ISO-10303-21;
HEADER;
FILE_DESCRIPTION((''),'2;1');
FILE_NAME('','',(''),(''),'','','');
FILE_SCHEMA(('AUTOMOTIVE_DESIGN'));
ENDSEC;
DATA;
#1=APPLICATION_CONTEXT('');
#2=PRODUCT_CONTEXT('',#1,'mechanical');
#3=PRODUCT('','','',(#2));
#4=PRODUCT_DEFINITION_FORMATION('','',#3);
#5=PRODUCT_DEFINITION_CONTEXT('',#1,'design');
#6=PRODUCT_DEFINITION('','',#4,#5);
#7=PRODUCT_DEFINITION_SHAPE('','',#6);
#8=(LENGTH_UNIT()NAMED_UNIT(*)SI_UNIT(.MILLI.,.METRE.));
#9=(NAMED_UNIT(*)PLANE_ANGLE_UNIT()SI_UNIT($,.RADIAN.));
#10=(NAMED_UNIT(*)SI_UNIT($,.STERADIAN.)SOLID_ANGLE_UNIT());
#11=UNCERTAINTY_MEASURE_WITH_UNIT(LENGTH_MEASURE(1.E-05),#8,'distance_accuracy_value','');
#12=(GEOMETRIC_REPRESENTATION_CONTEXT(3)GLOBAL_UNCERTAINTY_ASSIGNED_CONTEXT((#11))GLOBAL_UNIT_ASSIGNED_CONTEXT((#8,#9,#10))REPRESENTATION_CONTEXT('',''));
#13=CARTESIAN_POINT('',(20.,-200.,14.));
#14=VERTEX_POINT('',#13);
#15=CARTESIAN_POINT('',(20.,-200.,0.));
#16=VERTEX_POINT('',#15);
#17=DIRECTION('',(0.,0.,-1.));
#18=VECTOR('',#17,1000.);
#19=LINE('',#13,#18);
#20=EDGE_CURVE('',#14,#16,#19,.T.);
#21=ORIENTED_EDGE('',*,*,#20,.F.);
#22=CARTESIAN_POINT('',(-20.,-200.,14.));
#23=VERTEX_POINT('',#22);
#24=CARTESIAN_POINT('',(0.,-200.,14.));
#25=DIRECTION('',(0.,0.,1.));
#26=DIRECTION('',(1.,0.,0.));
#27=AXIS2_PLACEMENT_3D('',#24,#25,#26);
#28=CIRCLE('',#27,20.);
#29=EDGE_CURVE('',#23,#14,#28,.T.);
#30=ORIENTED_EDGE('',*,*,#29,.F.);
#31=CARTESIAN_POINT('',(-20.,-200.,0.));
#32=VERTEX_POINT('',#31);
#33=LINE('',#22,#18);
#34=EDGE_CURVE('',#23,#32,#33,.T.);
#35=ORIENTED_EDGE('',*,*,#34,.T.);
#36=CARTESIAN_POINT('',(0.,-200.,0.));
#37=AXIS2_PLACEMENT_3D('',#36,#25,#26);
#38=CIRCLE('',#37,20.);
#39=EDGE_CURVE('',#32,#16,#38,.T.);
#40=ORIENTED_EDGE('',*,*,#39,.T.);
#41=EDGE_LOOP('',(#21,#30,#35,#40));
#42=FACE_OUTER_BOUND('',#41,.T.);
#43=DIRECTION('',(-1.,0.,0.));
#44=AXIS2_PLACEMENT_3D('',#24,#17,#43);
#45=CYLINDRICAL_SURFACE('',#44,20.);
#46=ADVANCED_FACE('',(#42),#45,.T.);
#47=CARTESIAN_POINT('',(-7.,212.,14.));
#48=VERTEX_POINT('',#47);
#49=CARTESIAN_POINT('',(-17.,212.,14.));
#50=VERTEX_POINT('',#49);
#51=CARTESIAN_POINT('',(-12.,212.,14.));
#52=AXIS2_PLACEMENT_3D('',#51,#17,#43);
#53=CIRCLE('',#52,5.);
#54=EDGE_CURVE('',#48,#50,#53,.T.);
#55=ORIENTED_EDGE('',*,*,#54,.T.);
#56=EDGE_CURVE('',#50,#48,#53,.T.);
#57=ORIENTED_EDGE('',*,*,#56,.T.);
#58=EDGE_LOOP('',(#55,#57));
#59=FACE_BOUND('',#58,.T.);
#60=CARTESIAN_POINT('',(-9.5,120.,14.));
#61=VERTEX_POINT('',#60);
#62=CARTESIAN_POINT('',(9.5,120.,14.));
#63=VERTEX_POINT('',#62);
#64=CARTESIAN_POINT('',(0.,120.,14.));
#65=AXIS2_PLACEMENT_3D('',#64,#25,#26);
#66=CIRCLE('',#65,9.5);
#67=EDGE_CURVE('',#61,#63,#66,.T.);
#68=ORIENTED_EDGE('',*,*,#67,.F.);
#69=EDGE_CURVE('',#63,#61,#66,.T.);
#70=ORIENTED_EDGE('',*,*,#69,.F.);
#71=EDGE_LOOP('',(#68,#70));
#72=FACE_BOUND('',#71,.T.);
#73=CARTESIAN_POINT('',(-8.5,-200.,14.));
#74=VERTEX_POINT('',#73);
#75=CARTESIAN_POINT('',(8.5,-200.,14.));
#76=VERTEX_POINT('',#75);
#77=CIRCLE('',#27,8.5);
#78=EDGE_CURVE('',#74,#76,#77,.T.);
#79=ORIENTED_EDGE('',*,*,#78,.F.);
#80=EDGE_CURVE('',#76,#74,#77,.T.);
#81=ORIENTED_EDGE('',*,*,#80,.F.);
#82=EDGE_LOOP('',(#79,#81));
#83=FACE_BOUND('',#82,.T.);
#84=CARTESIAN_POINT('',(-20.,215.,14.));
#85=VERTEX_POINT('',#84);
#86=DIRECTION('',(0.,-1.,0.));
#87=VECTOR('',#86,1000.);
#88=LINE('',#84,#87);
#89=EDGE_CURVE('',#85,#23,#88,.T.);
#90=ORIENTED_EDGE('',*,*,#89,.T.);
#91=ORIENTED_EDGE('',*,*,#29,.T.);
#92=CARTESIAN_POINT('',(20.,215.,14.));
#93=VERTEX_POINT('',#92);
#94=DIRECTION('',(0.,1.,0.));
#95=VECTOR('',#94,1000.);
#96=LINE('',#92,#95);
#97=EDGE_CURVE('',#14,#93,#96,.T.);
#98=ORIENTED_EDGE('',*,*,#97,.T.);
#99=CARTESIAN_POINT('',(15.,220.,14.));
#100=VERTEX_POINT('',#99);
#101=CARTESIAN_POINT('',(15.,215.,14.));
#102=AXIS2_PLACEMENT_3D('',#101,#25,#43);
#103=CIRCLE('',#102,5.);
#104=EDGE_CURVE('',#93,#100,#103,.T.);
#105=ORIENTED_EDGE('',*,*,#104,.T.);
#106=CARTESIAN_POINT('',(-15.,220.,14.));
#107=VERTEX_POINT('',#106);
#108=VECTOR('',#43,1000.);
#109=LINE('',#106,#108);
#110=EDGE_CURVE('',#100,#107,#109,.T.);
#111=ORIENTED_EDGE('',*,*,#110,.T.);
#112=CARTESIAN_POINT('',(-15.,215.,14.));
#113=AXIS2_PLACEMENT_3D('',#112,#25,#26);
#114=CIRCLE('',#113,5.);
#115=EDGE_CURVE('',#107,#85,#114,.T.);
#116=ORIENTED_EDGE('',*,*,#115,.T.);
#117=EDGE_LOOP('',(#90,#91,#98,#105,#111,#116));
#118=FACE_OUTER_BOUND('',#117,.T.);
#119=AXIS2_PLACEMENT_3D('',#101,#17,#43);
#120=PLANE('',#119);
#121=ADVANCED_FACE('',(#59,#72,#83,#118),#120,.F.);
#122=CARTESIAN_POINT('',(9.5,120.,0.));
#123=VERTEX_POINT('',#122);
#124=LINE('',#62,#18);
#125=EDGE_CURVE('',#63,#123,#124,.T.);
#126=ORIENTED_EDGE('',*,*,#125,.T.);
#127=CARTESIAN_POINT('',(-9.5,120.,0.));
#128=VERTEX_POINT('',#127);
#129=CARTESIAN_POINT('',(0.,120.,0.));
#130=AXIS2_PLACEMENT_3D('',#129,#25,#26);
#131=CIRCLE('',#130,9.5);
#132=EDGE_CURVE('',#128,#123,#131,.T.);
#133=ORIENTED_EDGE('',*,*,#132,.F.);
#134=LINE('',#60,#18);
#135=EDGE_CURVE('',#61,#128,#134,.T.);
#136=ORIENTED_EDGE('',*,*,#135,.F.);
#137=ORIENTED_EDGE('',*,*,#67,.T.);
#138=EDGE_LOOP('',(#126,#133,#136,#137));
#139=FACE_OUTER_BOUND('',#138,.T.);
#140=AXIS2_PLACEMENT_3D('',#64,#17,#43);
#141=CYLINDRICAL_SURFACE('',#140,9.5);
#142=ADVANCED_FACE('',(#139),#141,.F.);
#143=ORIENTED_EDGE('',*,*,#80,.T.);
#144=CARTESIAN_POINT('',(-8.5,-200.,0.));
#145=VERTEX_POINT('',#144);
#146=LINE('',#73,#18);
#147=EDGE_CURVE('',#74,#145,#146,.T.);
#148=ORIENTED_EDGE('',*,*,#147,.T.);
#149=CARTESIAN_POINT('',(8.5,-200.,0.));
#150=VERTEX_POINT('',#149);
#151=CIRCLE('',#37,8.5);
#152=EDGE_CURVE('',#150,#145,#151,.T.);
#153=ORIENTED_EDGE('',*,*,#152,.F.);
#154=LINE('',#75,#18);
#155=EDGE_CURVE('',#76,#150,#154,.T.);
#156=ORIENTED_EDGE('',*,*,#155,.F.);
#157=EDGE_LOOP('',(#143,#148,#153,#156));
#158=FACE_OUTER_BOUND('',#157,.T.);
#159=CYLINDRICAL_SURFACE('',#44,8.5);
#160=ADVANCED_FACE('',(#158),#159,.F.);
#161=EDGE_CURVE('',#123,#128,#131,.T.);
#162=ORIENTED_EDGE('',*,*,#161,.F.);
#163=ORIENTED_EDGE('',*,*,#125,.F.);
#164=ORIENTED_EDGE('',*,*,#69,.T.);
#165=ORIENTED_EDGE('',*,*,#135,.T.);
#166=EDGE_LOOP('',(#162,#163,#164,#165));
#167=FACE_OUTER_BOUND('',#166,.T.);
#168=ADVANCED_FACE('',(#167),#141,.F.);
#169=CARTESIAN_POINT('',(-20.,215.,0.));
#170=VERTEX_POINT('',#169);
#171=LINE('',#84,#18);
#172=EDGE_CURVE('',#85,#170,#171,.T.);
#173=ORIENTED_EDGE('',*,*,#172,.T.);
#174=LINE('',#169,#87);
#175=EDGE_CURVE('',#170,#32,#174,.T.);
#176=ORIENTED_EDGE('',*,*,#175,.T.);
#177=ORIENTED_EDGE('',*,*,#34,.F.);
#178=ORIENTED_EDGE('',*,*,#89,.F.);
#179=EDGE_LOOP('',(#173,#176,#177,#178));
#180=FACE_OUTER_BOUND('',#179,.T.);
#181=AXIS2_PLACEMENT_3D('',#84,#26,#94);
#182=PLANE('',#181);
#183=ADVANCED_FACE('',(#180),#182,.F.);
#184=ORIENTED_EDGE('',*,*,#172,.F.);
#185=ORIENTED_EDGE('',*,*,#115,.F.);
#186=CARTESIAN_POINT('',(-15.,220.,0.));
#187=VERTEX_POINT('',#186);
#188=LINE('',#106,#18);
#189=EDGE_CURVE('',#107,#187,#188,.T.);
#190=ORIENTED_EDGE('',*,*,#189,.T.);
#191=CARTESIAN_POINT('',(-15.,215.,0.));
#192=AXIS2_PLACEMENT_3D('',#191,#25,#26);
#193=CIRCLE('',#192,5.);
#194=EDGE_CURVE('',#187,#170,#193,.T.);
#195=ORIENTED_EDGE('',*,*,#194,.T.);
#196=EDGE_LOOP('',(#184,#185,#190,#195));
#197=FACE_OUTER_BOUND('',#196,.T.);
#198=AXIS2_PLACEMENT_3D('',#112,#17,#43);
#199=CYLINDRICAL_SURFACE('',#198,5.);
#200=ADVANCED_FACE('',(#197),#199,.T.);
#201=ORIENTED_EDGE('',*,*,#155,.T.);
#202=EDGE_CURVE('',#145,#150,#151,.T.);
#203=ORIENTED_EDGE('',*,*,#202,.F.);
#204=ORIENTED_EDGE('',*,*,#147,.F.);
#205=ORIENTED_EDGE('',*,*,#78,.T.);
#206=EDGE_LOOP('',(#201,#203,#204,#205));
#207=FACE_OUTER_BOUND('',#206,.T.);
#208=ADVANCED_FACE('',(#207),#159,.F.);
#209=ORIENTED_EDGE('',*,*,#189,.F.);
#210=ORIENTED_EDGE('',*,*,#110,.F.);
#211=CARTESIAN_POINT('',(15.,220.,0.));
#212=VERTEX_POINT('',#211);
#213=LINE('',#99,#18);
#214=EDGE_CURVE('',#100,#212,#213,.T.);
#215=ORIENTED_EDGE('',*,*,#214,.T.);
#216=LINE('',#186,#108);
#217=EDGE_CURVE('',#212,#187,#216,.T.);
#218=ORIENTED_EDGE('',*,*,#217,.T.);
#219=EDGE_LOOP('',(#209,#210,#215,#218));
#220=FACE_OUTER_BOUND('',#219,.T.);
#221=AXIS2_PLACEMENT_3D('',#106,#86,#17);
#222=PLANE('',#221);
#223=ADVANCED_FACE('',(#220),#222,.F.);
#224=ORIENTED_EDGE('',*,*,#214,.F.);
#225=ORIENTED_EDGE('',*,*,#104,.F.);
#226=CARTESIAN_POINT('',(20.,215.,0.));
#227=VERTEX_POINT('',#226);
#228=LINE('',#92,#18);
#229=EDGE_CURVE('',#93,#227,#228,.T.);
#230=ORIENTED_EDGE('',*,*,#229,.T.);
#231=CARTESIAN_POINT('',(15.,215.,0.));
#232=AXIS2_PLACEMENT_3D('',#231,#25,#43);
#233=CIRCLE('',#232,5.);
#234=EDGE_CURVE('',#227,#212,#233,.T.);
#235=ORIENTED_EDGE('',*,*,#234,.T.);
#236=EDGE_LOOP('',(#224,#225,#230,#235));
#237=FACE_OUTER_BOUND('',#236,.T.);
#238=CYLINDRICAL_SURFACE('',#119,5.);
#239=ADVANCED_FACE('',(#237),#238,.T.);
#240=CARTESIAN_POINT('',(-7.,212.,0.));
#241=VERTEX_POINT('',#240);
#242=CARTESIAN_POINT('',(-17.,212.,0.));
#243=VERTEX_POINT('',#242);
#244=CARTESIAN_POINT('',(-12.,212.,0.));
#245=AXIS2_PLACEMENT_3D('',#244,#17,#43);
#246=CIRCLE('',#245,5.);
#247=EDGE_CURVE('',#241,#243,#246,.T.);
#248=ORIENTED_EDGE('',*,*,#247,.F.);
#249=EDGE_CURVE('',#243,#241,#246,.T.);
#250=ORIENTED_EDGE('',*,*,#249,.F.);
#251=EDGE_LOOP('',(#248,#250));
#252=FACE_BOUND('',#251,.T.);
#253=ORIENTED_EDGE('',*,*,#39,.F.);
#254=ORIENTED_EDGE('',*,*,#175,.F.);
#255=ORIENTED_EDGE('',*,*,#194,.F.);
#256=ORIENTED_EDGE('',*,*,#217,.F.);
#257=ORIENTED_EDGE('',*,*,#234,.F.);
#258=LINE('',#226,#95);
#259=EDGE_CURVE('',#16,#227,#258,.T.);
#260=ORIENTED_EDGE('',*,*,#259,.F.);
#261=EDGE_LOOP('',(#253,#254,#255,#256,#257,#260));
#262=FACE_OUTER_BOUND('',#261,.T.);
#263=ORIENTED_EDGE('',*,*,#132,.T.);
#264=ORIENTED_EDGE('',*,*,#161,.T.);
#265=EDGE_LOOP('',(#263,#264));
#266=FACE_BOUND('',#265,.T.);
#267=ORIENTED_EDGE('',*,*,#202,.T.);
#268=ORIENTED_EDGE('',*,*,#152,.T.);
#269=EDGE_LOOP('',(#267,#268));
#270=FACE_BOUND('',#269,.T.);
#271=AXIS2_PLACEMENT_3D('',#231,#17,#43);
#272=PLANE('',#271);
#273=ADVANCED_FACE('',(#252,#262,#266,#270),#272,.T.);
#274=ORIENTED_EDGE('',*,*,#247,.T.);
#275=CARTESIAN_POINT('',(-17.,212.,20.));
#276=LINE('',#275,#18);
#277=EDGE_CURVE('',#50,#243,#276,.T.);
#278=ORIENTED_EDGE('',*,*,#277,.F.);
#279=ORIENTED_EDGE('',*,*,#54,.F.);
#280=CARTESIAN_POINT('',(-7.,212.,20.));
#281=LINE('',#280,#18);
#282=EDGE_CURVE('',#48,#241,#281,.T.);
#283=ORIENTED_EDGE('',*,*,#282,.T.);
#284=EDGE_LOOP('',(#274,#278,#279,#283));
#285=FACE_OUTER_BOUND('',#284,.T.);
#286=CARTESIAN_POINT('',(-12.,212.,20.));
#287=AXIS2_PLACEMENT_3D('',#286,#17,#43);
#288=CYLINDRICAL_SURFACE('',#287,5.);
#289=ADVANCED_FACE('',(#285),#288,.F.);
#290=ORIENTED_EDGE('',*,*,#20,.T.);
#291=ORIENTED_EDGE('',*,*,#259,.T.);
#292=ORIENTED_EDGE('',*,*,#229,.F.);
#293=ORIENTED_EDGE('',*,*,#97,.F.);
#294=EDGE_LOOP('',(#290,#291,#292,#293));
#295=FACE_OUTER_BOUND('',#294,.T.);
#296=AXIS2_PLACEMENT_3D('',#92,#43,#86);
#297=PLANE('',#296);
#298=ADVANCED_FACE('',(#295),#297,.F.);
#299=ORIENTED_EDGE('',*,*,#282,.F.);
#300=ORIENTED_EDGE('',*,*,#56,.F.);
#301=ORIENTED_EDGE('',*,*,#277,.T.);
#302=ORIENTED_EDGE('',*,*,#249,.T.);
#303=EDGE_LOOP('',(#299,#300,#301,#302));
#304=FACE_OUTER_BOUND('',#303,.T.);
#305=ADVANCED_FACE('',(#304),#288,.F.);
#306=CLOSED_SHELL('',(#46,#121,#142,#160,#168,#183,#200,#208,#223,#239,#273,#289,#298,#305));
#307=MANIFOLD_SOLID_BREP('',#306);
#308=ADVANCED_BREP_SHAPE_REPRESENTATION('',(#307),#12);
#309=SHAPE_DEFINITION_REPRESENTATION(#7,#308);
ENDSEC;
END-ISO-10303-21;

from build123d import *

# Parameters (mm, degrees)
SKETCH_1_R          = 9.5
SKETCH_1_R_2        = 8.5
EXTRUDE_1_DEPTH     = 14
SKETCH_2_R          = 5
CUT_EXTRUDE_1_DEPTH = 20


with BuildPart() as part:
    # 草图1 → 凸台-拉伸1 (new body)
    with BuildSketch(Plane.XY):
        with BuildLine():
            Line((-15, 220), (15, 220))
            ThreePointArc((15, 220), (18.535533906, 218.535533906), (20, 215))
            Line((20, 215), (20, -200))
            ThreePointArc((20, -200), (0, -220), (-20, -200))
            Line((-20, -200), (-20, 215))
            ThreePointArc((-20, 215), (-18.535533906, 218.535533906), (-15, 220))
        make_face()
        with Locations((0, 120)):
            Circle(SKETCH_1_R, mode=Mode.SUBTRACT)
        with Locations((0, -200)):
            Circle(SKETCH_1_R_2, mode=Mode.SUBTRACT)
    extrude(amount=EXTRUDE_1_DEPTH)

    # 草图2 → 切除-拉伸1 (cut)
    with BuildSketch(Plane(origin=(0, 0, 0), x_dir=(-1, 0, 0), z_dir=(0, 0, -1))):
        with Locations((12, 212)):
            Circle(SKETCH_2_R)
    extrude(amount=-CUT_EXTRUDE_1_DEPTH, mode=Mode.SUBTRACT)


solid = part.part
